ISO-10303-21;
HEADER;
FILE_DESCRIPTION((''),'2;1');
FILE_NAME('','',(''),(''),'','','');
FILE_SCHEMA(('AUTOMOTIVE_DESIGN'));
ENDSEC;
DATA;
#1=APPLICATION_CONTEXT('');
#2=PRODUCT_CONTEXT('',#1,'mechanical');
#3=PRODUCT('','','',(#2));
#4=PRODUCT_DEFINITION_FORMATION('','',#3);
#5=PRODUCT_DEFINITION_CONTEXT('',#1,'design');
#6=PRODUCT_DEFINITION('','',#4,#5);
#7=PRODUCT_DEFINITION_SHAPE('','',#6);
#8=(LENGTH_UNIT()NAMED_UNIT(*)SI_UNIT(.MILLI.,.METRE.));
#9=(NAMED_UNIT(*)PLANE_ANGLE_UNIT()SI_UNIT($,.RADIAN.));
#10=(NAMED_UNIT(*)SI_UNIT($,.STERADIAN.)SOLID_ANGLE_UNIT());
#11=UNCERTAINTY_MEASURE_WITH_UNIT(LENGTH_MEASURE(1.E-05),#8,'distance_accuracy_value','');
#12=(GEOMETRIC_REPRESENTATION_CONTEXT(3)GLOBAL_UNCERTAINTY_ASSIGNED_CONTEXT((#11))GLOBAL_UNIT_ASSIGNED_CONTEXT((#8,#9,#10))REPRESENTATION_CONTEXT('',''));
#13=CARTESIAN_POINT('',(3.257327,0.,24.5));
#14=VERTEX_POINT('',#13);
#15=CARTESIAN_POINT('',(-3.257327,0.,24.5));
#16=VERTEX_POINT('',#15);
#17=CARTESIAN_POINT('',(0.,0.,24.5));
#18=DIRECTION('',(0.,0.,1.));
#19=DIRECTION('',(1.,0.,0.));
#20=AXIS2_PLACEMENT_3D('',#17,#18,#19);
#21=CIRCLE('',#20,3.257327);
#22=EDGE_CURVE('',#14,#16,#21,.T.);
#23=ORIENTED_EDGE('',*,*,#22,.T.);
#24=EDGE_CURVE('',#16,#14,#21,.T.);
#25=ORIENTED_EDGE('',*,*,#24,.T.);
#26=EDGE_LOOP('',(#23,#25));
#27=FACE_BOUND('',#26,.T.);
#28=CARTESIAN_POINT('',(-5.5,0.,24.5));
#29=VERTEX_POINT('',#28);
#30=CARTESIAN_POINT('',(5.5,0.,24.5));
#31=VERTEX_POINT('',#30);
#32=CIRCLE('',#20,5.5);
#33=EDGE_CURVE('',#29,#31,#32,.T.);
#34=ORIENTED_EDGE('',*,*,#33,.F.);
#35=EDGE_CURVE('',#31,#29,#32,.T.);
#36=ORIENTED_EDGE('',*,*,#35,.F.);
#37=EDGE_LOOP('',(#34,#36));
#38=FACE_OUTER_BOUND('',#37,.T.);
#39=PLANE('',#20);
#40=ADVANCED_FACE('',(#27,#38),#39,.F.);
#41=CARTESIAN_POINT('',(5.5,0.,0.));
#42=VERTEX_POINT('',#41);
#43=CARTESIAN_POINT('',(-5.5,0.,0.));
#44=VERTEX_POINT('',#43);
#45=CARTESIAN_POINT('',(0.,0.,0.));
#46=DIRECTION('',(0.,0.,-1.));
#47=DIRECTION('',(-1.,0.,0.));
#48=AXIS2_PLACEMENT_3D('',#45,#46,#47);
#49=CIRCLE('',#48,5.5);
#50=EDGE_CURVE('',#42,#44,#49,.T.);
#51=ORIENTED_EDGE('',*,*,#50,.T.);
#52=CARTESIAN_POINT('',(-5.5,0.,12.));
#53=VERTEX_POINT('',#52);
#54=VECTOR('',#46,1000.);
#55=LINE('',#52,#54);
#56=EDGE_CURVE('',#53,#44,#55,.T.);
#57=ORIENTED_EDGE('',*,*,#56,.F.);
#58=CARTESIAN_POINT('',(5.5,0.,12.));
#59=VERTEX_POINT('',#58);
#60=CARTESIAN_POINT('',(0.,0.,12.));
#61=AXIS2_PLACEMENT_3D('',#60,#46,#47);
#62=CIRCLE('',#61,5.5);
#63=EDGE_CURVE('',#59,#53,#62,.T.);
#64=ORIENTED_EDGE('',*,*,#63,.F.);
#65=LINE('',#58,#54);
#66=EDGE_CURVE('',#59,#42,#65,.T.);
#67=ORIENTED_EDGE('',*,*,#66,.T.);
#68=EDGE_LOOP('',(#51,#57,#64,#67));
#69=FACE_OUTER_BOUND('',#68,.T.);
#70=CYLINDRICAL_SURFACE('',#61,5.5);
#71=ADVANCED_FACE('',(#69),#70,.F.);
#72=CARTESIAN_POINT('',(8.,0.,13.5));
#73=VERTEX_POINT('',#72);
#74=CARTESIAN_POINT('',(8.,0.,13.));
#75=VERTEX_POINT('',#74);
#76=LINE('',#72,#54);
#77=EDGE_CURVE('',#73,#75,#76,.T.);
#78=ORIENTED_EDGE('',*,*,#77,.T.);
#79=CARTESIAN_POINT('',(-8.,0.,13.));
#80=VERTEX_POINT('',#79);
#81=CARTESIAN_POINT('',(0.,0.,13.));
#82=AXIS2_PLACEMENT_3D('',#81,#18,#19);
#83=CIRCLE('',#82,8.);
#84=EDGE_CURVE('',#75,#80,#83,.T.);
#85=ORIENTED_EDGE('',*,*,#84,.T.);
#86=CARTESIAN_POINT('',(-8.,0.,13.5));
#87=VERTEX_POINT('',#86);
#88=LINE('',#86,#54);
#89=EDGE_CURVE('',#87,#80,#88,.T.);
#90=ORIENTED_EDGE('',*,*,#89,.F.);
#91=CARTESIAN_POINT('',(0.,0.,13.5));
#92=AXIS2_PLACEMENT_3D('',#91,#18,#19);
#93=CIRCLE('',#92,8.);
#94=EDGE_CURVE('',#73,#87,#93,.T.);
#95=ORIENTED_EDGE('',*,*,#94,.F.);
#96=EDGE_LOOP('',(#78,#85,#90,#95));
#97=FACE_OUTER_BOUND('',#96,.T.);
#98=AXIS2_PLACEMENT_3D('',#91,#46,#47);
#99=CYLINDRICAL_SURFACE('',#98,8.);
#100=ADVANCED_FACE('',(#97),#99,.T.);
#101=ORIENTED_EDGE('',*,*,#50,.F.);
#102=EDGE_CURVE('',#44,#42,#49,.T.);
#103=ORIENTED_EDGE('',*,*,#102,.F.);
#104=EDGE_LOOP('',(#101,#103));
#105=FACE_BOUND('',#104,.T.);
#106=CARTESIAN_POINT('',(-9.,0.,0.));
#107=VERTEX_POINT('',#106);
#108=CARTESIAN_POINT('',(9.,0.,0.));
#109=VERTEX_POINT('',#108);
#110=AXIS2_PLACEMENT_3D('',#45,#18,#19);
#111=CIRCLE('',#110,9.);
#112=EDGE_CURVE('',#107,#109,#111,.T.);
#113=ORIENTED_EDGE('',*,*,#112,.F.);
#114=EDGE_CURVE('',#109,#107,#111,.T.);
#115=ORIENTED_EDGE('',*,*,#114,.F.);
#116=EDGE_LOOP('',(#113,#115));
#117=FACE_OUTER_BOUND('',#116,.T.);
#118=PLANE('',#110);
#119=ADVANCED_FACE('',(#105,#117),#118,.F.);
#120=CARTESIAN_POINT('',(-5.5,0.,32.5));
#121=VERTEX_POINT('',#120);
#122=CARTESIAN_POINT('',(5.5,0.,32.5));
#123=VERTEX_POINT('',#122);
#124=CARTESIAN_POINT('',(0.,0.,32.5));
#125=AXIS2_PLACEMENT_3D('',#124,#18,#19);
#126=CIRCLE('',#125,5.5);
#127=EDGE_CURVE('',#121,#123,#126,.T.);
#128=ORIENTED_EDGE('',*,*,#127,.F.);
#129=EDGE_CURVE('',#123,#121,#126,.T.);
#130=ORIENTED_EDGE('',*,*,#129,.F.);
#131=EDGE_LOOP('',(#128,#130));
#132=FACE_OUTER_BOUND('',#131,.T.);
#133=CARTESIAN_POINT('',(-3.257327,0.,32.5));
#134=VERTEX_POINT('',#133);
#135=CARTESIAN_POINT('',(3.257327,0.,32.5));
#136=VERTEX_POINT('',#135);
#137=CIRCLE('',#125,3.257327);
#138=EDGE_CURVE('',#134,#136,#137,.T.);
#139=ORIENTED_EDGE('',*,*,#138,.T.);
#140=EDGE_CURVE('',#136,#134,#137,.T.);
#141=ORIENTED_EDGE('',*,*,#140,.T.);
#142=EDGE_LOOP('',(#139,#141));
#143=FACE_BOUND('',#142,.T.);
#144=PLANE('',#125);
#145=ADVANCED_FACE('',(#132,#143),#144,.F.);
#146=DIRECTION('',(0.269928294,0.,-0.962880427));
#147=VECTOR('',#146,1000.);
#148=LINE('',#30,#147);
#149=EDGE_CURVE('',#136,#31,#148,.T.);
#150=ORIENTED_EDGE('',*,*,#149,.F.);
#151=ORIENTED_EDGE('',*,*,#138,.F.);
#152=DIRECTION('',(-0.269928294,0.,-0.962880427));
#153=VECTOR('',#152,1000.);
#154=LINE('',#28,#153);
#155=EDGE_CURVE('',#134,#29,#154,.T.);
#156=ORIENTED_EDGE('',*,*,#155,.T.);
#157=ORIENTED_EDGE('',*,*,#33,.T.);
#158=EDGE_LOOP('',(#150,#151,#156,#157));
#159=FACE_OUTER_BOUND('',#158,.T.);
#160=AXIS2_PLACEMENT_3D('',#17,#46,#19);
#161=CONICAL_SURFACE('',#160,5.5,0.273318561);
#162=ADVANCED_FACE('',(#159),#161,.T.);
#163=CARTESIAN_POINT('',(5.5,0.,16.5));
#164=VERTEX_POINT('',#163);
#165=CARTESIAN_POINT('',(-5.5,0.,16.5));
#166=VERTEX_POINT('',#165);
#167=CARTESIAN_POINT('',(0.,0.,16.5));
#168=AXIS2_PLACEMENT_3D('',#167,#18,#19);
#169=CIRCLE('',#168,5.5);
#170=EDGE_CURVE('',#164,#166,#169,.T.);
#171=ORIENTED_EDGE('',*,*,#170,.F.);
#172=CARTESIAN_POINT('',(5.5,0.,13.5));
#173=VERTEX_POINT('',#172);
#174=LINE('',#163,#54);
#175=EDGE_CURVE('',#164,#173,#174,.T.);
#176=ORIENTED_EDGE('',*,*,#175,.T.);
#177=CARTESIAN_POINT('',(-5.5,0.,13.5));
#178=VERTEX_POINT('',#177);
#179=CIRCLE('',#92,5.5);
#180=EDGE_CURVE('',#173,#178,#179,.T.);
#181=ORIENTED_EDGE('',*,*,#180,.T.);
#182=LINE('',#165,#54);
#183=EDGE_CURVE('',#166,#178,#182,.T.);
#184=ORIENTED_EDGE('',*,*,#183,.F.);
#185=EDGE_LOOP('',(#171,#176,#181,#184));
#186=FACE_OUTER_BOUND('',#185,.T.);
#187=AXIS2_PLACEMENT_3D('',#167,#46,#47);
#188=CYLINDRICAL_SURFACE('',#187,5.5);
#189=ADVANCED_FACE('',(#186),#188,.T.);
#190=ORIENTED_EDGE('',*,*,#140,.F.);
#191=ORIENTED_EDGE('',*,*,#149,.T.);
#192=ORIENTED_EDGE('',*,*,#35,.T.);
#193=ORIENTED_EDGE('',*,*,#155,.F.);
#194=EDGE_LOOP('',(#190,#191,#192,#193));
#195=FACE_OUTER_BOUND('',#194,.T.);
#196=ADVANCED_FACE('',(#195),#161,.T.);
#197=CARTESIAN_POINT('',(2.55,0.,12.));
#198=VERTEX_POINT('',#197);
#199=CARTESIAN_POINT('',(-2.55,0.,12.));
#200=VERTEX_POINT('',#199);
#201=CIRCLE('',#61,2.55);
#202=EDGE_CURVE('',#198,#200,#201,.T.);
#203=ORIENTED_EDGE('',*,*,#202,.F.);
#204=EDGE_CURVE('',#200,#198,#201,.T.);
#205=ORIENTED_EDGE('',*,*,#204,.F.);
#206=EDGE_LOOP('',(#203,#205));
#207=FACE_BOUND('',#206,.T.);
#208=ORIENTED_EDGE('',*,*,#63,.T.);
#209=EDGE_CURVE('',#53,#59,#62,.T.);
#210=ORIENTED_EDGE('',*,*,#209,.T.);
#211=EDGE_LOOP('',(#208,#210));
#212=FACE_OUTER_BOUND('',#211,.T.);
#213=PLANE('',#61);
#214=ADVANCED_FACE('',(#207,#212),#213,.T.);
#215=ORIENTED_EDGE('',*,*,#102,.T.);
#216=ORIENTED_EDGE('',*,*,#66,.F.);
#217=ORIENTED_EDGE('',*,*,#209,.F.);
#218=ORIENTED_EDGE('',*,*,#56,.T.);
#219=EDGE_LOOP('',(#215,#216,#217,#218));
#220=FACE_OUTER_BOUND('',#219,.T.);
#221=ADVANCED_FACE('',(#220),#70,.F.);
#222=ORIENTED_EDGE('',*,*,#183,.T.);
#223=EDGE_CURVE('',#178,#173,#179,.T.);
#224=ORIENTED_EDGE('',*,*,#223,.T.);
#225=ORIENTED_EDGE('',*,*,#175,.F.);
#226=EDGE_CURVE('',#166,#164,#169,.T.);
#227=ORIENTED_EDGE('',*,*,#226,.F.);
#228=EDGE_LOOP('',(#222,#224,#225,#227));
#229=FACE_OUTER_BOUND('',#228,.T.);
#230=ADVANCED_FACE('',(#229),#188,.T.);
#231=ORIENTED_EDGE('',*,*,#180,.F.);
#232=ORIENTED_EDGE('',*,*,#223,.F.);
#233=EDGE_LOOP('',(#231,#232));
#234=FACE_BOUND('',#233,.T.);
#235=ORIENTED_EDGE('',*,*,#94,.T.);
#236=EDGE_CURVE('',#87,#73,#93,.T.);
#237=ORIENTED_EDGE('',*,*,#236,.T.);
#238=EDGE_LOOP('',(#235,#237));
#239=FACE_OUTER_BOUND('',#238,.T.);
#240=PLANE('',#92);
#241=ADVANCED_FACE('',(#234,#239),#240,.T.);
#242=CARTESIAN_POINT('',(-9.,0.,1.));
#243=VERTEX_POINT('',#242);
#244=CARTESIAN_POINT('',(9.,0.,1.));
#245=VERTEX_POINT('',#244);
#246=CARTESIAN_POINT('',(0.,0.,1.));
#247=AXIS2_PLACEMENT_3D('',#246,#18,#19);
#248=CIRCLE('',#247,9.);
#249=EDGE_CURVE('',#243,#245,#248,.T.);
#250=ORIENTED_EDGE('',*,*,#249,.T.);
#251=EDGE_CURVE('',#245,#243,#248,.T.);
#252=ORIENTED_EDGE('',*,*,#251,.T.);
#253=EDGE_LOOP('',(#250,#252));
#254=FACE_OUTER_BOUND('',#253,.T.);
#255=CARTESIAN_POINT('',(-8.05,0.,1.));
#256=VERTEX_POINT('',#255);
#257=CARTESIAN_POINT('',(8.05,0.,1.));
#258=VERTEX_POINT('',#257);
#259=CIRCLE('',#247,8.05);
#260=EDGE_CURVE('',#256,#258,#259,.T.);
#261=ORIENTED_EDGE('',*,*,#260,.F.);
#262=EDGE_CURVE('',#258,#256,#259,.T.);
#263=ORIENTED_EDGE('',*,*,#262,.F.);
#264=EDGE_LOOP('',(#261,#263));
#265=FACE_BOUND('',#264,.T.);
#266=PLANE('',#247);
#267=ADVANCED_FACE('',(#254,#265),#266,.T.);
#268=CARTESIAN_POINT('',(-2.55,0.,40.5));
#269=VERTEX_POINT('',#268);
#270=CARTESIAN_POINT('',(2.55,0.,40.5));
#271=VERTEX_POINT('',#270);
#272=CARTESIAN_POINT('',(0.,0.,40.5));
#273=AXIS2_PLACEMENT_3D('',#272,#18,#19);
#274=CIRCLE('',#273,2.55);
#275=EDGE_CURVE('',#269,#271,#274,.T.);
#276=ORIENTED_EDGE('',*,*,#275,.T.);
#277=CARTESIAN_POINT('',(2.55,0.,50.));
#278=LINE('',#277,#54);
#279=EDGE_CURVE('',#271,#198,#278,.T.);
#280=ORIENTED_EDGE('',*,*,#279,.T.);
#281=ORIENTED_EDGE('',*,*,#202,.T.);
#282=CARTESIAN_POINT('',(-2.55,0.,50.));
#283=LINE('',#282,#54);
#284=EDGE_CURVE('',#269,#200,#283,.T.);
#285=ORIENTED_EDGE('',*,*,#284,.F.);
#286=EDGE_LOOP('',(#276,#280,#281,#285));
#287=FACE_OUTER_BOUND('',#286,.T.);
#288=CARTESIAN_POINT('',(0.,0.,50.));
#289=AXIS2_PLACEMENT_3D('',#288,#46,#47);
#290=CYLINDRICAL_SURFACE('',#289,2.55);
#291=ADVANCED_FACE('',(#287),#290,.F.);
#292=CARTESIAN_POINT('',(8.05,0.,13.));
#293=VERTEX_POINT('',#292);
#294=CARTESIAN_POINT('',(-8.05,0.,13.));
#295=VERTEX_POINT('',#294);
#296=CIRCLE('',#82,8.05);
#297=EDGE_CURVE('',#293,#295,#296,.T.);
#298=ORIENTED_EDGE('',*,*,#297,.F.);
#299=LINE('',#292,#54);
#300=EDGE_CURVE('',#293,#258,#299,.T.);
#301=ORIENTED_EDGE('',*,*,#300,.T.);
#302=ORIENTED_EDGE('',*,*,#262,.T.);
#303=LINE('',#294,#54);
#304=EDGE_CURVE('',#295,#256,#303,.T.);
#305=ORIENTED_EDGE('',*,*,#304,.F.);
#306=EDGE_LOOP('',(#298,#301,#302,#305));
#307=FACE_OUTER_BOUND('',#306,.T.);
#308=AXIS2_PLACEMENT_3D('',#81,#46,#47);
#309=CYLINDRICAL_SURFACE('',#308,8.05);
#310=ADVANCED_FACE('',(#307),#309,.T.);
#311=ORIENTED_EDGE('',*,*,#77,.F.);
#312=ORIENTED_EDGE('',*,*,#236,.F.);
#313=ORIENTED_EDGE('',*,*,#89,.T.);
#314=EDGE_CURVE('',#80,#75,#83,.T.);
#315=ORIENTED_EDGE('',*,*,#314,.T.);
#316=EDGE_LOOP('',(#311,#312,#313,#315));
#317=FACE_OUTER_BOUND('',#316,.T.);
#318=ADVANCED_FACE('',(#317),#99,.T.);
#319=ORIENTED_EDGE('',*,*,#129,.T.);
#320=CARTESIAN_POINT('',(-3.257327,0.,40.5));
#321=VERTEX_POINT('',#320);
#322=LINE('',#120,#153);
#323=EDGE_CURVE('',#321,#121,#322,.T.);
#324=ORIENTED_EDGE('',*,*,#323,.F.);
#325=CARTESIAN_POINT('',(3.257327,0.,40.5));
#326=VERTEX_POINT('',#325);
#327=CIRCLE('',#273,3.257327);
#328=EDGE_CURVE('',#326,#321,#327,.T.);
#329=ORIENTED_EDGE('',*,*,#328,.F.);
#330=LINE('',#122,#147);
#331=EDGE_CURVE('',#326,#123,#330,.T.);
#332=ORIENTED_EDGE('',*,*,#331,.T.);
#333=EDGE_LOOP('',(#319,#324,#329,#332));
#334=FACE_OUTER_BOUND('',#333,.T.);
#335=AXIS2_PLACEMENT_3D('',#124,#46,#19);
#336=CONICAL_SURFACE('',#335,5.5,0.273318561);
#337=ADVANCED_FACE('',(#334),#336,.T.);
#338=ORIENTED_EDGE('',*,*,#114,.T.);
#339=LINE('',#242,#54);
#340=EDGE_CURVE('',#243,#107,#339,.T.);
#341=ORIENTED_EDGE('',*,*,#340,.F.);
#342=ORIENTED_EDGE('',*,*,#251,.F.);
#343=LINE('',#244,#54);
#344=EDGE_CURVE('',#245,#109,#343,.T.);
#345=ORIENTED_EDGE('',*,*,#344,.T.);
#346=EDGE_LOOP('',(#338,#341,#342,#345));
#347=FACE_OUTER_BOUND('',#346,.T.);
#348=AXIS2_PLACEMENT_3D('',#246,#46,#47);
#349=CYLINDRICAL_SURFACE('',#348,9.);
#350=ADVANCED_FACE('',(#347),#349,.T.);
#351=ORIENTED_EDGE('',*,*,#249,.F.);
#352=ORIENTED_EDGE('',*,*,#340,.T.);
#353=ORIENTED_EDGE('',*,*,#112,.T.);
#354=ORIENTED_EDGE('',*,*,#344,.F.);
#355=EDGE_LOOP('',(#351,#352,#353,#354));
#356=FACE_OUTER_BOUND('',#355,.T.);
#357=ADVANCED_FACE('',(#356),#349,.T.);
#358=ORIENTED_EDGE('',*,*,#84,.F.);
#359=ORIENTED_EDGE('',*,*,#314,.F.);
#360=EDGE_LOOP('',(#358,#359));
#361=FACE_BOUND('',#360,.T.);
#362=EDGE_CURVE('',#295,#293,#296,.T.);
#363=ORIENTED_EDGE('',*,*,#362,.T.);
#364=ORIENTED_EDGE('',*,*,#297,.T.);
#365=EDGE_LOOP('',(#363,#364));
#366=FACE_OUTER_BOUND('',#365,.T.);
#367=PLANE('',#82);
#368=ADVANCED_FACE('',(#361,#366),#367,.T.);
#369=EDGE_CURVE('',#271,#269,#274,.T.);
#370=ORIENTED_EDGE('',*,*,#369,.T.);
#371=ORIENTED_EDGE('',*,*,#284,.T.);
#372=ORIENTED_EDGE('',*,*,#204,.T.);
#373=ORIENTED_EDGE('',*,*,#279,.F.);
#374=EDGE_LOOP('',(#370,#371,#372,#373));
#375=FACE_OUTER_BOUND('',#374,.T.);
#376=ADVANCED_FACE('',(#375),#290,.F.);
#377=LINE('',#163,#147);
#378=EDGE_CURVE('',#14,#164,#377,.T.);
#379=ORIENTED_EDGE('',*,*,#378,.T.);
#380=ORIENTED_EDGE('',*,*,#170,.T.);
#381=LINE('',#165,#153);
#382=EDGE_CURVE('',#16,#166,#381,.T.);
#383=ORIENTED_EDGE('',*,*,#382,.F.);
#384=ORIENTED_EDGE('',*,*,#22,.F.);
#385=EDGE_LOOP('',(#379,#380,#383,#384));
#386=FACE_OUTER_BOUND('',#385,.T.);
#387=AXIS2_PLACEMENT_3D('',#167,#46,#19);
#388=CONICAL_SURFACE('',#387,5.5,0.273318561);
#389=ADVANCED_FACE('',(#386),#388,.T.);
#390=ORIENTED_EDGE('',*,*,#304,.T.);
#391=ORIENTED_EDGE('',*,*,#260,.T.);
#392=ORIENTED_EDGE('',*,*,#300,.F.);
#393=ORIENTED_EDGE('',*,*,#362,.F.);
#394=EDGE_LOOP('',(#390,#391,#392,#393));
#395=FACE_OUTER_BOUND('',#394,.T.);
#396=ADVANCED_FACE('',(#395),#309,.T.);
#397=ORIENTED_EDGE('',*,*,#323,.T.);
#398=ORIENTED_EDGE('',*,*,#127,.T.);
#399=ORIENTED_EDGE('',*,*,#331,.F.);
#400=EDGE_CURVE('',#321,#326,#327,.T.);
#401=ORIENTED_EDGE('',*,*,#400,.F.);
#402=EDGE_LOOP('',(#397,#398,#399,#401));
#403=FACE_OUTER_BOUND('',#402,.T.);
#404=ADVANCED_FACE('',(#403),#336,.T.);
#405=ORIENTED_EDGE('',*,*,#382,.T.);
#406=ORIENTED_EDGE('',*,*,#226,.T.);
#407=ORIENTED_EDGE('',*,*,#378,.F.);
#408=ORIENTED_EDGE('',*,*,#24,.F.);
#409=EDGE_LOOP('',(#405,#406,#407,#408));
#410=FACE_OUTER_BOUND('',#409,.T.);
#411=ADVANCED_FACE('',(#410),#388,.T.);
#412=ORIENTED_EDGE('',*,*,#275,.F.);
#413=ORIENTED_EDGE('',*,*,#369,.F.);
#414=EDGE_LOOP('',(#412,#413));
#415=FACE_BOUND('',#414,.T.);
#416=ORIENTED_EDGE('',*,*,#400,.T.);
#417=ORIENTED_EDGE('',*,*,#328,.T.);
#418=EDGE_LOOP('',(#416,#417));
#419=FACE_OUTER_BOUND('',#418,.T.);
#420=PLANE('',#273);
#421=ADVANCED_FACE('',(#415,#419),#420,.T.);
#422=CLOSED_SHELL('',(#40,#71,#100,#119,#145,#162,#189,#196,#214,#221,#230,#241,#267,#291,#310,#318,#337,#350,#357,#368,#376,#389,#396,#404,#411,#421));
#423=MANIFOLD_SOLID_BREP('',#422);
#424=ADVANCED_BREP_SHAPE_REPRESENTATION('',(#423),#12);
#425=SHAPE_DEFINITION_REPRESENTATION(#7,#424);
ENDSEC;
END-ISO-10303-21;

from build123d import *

# Parameters (mm, degrees)
FLANGE_SKETCH_R        = 9
FLANGE_DEPTH           = 1
BODY_SKETCH_R          = 8.05
BODY_DEPTH             = 12
SHOULDER_STEP_SKETCH_R = 8
SHOULDER_STEP_DEPTH    = 0.5
NECK_SKETCH_R          = 5.5
NECK_DEPTH             = 3
BARB_1_SKETCH_R        = 5.5
BARB_1_DEPTH           = 8
BARB_1_TAPER           = 15.66
BARB_2_SKETCH_R        = 5.5
BARB_2_DEPTH           = 8
BARB_2_TAPER           = 15.66
BARB_3_SKETCH_R        = 5.5
BARB_3_TIP_DEPTH       = 8
BARB_3_TIP_TAPER       = 15.66
INLET_BORE_SKETCH_R    = 5.5
INLET_BORE_DEPTH       = 12
THROUGH_BORE_SKETCH_R  = 2.55
THROUGH_BORE_DEPTH     = 38


with BuildPart() as part:
    # Flange Sketch → Flange (new body)
    with BuildSketch(Plane.XY):
        Circle(FLANGE_SKETCH_R)
    extrude(amount=FLANGE_DEPTH)

    # Body Sketch → Body (add)
    with BuildSketch(Plane.XY.offset(1)):
        Circle(BODY_SKETCH_R)
    extrude(amount=BODY_DEPTH)

    # Shoulder Step Sketch → Shoulder Step (add)
    with BuildSketch(Plane.XY.offset(13)):
        Circle(SHOULDER_STEP_SKETCH_R)
    extrude(amount=SHOULDER_STEP_DEPTH)

    # Neck Sketch → Neck (add)
    with BuildSketch(Plane.XY.offset(13.5)):
        Circle(NECK_SKETCH_R)
    extrude(amount=NECK_DEPTH)

    # Barb 1 Sketch → Barb 1 (add)
    with BuildSketch(Plane.XY.offset(16.5)):
        Circle(BARB_1_SKETCH_R)
    extrude(amount=BARB_1_DEPTH, taper=BARB_1_TAPER)

    # Barb 2 Sketch → Barb 2 (add)
    with BuildSketch(Plane.XY.offset(24.5)):
        Circle(BARB_2_SKETCH_R)
    extrude(amount=BARB_2_DEPTH, taper=BARB_2_TAPER)

    # Barb 3 Sketch → Barb 3 Tip (add)
    with BuildSketch(Plane.XY.offset(32.5)):
        Circle(BARB_3_SKETCH_R)
    extrude(amount=BARB_3_TIP_DEPTH, taper=BARB_3_TIP_TAPER)

    # Inlet Bore Sketch → Inlet Bore (cut)
    with BuildSketch(Plane(origin=(0, 0, 0), x_dir=(-1, 0, 0), z_dir=(0, 0, -1))):
        with Locations(Location((0, 0, 0), (0, 0, 180))):
            Circle(INLET_BORE_SKETCH_R)
    extrude(amount=-INLET_BORE_DEPTH, mode=Mode.SUBTRACT)

    # Through Bore Sketch → Through Bore (cut)
    with BuildSketch(Plane(origin=(0, 0, 12), x_dir=(-1, 0, 0), z_dir=(0, 0, -1))):
        Circle(THROUGH_BORE_SKETCH_R)
    extrude(amount=-THROUGH_BORE_DEPTH, mode=Mode.SUBTRACT)


solid = part.part
